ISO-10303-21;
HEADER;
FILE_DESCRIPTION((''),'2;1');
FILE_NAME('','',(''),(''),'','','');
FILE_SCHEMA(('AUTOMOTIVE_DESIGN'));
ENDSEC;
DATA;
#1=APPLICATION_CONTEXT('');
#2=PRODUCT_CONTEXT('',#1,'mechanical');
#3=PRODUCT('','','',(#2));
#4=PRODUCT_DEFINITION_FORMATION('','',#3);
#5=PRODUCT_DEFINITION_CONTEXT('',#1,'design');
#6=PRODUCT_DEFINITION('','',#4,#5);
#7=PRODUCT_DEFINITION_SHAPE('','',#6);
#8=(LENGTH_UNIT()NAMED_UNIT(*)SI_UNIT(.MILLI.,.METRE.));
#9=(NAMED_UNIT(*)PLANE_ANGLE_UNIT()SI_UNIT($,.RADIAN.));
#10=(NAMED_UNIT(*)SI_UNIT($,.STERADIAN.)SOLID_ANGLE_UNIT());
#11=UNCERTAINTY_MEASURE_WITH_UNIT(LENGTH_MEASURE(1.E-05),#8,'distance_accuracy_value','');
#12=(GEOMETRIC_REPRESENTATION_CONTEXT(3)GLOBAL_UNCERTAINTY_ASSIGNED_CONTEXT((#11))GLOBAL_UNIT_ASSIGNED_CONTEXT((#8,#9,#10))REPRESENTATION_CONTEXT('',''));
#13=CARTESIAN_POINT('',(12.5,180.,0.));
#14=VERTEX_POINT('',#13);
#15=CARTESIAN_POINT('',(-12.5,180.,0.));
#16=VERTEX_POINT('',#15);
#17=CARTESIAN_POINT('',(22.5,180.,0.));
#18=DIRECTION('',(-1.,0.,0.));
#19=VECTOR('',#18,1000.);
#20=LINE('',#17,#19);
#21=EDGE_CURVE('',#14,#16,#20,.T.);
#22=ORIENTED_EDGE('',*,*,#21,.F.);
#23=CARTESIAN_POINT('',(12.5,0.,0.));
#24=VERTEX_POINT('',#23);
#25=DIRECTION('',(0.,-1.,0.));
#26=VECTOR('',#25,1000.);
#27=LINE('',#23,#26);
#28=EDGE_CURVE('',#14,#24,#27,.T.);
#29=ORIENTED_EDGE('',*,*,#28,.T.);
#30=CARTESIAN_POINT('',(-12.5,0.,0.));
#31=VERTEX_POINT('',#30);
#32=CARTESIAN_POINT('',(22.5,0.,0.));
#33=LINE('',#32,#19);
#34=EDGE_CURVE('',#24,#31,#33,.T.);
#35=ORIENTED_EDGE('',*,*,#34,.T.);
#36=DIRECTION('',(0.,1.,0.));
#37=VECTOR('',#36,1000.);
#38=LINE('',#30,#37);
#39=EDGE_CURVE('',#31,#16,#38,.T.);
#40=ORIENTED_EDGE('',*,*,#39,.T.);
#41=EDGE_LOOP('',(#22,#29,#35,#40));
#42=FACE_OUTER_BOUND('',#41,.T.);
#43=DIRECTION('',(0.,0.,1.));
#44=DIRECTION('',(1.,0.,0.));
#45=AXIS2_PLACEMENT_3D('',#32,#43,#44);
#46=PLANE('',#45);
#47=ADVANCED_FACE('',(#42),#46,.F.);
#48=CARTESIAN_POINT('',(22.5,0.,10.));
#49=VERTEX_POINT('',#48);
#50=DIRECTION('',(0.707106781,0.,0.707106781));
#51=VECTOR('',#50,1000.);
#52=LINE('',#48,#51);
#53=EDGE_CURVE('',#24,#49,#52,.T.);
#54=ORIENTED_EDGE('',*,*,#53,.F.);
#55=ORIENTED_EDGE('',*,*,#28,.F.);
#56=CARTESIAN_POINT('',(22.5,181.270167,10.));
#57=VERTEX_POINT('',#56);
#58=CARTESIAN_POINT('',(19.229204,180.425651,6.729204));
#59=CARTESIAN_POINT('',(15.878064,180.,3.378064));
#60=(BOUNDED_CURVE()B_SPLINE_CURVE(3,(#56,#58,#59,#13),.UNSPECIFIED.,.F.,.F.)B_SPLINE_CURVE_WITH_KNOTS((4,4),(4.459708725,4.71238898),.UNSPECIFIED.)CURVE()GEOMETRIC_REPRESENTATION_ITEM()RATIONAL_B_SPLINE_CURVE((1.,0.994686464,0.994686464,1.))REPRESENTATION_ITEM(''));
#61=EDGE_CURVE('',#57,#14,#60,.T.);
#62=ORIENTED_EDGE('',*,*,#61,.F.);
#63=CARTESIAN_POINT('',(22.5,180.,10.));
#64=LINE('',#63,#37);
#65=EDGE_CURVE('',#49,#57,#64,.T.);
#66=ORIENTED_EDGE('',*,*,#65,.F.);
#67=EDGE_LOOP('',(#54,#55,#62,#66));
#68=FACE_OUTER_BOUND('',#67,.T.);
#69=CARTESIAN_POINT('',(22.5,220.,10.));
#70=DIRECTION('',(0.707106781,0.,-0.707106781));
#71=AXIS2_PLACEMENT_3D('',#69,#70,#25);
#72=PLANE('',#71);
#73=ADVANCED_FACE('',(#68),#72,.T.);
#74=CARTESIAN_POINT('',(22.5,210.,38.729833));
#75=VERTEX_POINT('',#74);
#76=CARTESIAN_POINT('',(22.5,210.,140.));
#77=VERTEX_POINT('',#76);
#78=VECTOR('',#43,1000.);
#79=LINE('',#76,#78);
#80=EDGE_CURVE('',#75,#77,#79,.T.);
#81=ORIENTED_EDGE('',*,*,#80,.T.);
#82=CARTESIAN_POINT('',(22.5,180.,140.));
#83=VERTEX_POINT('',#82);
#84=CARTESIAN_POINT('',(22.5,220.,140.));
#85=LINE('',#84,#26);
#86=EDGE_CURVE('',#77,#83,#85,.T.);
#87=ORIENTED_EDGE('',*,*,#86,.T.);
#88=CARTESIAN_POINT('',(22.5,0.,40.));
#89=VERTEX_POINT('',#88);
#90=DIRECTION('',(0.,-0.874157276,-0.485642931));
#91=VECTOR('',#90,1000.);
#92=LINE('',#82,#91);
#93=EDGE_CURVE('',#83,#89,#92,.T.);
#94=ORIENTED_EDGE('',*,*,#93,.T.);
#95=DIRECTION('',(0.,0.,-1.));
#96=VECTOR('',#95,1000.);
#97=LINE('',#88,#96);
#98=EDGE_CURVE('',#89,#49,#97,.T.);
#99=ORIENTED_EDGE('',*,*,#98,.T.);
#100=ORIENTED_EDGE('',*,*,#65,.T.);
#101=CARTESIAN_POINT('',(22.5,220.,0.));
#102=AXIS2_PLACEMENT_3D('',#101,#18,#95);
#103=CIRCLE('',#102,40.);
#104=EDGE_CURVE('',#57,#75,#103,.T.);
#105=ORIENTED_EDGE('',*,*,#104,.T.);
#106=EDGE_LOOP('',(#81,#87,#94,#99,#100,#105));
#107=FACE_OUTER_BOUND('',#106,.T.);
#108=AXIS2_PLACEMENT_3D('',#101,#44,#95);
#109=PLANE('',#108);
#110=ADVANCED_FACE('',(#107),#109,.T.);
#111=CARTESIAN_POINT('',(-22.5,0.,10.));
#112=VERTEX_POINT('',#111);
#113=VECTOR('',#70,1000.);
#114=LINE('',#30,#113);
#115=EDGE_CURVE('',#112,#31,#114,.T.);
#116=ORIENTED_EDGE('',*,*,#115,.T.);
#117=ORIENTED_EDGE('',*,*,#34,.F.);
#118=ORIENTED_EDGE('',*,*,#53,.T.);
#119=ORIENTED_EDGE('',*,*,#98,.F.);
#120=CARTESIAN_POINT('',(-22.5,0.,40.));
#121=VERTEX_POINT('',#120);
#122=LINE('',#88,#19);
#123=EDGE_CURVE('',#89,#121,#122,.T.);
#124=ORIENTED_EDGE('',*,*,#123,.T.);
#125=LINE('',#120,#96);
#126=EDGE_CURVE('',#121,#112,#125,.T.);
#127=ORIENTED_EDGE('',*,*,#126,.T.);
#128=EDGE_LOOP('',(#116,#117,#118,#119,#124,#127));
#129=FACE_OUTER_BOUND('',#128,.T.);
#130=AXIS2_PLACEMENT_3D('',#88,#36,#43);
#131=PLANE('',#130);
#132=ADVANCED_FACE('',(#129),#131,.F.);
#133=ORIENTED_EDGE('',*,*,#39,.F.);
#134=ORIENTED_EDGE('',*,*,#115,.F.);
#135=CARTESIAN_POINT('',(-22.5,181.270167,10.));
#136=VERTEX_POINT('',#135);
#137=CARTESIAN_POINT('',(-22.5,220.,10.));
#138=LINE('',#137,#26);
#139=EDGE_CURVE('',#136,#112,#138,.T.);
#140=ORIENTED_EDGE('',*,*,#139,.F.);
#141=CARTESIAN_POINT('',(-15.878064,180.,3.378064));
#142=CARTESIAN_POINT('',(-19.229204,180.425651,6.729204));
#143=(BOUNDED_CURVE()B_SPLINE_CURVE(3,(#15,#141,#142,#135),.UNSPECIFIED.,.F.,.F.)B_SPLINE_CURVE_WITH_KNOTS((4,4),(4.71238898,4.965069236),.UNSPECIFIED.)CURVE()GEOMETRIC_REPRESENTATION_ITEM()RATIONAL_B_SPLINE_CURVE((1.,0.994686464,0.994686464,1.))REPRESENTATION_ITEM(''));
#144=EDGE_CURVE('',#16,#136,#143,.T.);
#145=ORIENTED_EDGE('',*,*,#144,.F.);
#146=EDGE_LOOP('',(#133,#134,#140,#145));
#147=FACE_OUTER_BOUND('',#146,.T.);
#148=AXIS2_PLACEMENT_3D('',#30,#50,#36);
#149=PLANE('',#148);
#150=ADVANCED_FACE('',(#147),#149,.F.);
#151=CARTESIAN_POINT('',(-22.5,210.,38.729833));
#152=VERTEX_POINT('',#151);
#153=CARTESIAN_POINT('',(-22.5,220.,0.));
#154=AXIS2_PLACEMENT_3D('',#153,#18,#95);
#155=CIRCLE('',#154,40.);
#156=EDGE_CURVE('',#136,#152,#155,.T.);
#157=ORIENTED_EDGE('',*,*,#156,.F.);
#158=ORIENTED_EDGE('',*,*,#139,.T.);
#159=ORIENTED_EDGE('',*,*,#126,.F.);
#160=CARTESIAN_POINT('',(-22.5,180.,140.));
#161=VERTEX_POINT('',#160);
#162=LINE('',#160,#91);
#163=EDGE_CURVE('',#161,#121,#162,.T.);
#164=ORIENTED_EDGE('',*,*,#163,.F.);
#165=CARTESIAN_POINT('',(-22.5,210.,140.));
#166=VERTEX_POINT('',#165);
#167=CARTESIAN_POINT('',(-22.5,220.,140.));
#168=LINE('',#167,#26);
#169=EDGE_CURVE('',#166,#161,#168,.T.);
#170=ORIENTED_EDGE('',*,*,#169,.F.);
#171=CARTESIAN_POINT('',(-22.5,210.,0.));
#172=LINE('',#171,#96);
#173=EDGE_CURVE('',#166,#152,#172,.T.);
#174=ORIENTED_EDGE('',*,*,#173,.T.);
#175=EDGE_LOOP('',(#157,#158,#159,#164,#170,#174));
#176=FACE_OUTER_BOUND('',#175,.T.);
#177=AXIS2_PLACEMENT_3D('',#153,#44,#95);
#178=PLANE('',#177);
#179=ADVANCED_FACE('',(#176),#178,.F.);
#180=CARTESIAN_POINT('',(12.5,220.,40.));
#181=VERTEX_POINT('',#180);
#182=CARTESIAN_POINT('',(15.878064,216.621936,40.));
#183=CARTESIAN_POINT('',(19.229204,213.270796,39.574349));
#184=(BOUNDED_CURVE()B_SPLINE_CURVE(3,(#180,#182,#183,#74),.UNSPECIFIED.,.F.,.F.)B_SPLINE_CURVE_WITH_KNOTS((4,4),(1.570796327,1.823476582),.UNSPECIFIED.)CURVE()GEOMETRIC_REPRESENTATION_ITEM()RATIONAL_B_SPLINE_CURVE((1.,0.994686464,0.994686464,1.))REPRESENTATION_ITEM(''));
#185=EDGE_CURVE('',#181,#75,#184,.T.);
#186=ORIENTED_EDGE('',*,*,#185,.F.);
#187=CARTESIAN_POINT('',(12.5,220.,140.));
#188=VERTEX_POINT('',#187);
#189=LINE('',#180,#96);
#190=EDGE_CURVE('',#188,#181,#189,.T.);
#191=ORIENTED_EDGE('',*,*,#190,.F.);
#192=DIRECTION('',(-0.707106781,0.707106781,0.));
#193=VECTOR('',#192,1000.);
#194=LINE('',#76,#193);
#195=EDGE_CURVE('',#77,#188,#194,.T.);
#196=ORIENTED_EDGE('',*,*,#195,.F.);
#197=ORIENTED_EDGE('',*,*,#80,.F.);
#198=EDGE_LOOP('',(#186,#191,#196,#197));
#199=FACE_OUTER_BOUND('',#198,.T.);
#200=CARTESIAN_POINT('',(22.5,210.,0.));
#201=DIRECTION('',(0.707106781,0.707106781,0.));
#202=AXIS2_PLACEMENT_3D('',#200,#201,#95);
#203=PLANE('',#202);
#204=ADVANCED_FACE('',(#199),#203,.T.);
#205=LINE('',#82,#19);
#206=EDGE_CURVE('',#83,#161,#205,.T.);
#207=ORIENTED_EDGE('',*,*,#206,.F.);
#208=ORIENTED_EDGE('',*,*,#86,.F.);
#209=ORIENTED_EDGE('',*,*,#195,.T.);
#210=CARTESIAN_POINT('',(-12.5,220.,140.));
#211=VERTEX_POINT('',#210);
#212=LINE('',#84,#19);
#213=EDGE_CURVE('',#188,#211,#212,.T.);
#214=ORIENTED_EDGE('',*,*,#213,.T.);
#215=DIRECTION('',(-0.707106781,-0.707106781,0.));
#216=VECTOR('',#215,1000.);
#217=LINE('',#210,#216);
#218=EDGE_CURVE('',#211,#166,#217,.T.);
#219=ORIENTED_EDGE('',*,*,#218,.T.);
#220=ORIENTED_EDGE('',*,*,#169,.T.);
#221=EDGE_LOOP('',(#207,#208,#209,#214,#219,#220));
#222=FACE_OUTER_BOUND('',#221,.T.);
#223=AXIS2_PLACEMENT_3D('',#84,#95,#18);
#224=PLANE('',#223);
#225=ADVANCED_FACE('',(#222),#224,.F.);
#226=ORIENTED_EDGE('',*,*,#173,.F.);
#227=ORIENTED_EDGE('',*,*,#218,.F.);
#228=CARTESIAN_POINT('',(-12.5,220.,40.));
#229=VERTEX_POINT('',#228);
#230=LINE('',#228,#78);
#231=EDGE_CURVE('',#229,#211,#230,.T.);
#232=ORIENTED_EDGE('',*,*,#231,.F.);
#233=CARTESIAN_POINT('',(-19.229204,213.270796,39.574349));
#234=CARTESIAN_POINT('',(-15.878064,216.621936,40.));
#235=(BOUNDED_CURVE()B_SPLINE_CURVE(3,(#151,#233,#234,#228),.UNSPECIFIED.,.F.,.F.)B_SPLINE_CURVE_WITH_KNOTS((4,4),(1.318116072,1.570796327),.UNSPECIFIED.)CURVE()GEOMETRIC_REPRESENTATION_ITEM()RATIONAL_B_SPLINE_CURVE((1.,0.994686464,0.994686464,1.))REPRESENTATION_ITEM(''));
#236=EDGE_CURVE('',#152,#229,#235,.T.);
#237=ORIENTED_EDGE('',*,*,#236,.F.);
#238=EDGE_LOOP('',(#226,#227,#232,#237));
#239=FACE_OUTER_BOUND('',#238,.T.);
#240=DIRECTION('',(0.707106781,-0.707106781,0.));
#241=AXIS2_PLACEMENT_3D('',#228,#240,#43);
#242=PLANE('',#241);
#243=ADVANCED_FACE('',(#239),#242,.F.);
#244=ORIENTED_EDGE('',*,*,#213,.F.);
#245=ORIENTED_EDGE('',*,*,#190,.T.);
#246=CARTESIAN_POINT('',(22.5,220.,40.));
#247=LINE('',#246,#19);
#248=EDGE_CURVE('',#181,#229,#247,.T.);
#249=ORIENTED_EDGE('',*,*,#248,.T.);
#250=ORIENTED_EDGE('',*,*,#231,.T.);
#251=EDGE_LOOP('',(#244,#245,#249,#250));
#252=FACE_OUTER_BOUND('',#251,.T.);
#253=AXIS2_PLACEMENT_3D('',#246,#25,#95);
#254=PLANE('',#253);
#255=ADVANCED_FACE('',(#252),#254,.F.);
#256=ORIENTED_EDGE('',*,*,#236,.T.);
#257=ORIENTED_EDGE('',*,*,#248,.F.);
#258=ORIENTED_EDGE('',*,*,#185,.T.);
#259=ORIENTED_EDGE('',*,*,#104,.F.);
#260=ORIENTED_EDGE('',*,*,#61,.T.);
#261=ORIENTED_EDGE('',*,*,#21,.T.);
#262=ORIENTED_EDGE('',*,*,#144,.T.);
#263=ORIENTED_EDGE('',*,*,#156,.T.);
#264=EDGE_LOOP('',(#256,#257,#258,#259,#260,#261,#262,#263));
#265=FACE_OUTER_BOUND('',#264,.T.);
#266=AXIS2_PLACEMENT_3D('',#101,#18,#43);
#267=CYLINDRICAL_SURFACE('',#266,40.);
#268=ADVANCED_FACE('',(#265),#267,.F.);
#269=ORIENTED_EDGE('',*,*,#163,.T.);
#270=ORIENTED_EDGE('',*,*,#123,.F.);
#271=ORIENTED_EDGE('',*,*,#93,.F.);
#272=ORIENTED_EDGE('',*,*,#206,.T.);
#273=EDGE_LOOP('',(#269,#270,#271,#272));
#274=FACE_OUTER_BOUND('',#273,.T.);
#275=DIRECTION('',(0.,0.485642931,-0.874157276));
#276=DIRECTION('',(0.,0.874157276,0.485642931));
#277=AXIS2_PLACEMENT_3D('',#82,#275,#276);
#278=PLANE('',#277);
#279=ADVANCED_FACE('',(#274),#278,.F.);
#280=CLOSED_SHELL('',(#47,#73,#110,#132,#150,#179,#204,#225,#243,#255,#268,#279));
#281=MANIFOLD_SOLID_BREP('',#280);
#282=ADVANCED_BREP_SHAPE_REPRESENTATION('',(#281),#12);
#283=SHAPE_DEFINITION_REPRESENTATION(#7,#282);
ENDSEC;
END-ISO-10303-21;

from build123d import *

# Parameters (mm, degrees)
BOSS_EXTRUDE1_DEPTH = 22.5
CHAMFER1_SIZE       = 10


with BuildPart() as part:
    # Sketch1 → Boss-Extrude1 (new, symmetric)
    with BuildSketch(Plane(origin=(0, 0, 0), x_dir=(0, 0, -1), z_dir=(1, 0, 0))):
        with BuildLine():
            Line((0, 0), (0, 180))
            ThreePointArc((0, 180), (-28.284271247, 191.715728753), (-40, 220))
            Line((-40, 220), (-140, 220))
            Line((-140, 220), (-140, 180))
            Line((-140, 180), (-40, 0))
            Line((-40, 0), (0, 0))
        make_face()
    extrude(amount=BOSS_EXTRUDE1_DEPTH, both=True)

    # Chamfer1
    chamfer1_edges = [part.edges().sort_by_distance(p)[0] for p in [
        (22.5, 220, 90),
        (-22.5, 220, 90),
        (22.5, 90, 0),
        (-22.5, 90, 0),
    ]]
    chamfer(chamfer1_edges, length=CHAMFER1_SIZE)


solid = part.part
